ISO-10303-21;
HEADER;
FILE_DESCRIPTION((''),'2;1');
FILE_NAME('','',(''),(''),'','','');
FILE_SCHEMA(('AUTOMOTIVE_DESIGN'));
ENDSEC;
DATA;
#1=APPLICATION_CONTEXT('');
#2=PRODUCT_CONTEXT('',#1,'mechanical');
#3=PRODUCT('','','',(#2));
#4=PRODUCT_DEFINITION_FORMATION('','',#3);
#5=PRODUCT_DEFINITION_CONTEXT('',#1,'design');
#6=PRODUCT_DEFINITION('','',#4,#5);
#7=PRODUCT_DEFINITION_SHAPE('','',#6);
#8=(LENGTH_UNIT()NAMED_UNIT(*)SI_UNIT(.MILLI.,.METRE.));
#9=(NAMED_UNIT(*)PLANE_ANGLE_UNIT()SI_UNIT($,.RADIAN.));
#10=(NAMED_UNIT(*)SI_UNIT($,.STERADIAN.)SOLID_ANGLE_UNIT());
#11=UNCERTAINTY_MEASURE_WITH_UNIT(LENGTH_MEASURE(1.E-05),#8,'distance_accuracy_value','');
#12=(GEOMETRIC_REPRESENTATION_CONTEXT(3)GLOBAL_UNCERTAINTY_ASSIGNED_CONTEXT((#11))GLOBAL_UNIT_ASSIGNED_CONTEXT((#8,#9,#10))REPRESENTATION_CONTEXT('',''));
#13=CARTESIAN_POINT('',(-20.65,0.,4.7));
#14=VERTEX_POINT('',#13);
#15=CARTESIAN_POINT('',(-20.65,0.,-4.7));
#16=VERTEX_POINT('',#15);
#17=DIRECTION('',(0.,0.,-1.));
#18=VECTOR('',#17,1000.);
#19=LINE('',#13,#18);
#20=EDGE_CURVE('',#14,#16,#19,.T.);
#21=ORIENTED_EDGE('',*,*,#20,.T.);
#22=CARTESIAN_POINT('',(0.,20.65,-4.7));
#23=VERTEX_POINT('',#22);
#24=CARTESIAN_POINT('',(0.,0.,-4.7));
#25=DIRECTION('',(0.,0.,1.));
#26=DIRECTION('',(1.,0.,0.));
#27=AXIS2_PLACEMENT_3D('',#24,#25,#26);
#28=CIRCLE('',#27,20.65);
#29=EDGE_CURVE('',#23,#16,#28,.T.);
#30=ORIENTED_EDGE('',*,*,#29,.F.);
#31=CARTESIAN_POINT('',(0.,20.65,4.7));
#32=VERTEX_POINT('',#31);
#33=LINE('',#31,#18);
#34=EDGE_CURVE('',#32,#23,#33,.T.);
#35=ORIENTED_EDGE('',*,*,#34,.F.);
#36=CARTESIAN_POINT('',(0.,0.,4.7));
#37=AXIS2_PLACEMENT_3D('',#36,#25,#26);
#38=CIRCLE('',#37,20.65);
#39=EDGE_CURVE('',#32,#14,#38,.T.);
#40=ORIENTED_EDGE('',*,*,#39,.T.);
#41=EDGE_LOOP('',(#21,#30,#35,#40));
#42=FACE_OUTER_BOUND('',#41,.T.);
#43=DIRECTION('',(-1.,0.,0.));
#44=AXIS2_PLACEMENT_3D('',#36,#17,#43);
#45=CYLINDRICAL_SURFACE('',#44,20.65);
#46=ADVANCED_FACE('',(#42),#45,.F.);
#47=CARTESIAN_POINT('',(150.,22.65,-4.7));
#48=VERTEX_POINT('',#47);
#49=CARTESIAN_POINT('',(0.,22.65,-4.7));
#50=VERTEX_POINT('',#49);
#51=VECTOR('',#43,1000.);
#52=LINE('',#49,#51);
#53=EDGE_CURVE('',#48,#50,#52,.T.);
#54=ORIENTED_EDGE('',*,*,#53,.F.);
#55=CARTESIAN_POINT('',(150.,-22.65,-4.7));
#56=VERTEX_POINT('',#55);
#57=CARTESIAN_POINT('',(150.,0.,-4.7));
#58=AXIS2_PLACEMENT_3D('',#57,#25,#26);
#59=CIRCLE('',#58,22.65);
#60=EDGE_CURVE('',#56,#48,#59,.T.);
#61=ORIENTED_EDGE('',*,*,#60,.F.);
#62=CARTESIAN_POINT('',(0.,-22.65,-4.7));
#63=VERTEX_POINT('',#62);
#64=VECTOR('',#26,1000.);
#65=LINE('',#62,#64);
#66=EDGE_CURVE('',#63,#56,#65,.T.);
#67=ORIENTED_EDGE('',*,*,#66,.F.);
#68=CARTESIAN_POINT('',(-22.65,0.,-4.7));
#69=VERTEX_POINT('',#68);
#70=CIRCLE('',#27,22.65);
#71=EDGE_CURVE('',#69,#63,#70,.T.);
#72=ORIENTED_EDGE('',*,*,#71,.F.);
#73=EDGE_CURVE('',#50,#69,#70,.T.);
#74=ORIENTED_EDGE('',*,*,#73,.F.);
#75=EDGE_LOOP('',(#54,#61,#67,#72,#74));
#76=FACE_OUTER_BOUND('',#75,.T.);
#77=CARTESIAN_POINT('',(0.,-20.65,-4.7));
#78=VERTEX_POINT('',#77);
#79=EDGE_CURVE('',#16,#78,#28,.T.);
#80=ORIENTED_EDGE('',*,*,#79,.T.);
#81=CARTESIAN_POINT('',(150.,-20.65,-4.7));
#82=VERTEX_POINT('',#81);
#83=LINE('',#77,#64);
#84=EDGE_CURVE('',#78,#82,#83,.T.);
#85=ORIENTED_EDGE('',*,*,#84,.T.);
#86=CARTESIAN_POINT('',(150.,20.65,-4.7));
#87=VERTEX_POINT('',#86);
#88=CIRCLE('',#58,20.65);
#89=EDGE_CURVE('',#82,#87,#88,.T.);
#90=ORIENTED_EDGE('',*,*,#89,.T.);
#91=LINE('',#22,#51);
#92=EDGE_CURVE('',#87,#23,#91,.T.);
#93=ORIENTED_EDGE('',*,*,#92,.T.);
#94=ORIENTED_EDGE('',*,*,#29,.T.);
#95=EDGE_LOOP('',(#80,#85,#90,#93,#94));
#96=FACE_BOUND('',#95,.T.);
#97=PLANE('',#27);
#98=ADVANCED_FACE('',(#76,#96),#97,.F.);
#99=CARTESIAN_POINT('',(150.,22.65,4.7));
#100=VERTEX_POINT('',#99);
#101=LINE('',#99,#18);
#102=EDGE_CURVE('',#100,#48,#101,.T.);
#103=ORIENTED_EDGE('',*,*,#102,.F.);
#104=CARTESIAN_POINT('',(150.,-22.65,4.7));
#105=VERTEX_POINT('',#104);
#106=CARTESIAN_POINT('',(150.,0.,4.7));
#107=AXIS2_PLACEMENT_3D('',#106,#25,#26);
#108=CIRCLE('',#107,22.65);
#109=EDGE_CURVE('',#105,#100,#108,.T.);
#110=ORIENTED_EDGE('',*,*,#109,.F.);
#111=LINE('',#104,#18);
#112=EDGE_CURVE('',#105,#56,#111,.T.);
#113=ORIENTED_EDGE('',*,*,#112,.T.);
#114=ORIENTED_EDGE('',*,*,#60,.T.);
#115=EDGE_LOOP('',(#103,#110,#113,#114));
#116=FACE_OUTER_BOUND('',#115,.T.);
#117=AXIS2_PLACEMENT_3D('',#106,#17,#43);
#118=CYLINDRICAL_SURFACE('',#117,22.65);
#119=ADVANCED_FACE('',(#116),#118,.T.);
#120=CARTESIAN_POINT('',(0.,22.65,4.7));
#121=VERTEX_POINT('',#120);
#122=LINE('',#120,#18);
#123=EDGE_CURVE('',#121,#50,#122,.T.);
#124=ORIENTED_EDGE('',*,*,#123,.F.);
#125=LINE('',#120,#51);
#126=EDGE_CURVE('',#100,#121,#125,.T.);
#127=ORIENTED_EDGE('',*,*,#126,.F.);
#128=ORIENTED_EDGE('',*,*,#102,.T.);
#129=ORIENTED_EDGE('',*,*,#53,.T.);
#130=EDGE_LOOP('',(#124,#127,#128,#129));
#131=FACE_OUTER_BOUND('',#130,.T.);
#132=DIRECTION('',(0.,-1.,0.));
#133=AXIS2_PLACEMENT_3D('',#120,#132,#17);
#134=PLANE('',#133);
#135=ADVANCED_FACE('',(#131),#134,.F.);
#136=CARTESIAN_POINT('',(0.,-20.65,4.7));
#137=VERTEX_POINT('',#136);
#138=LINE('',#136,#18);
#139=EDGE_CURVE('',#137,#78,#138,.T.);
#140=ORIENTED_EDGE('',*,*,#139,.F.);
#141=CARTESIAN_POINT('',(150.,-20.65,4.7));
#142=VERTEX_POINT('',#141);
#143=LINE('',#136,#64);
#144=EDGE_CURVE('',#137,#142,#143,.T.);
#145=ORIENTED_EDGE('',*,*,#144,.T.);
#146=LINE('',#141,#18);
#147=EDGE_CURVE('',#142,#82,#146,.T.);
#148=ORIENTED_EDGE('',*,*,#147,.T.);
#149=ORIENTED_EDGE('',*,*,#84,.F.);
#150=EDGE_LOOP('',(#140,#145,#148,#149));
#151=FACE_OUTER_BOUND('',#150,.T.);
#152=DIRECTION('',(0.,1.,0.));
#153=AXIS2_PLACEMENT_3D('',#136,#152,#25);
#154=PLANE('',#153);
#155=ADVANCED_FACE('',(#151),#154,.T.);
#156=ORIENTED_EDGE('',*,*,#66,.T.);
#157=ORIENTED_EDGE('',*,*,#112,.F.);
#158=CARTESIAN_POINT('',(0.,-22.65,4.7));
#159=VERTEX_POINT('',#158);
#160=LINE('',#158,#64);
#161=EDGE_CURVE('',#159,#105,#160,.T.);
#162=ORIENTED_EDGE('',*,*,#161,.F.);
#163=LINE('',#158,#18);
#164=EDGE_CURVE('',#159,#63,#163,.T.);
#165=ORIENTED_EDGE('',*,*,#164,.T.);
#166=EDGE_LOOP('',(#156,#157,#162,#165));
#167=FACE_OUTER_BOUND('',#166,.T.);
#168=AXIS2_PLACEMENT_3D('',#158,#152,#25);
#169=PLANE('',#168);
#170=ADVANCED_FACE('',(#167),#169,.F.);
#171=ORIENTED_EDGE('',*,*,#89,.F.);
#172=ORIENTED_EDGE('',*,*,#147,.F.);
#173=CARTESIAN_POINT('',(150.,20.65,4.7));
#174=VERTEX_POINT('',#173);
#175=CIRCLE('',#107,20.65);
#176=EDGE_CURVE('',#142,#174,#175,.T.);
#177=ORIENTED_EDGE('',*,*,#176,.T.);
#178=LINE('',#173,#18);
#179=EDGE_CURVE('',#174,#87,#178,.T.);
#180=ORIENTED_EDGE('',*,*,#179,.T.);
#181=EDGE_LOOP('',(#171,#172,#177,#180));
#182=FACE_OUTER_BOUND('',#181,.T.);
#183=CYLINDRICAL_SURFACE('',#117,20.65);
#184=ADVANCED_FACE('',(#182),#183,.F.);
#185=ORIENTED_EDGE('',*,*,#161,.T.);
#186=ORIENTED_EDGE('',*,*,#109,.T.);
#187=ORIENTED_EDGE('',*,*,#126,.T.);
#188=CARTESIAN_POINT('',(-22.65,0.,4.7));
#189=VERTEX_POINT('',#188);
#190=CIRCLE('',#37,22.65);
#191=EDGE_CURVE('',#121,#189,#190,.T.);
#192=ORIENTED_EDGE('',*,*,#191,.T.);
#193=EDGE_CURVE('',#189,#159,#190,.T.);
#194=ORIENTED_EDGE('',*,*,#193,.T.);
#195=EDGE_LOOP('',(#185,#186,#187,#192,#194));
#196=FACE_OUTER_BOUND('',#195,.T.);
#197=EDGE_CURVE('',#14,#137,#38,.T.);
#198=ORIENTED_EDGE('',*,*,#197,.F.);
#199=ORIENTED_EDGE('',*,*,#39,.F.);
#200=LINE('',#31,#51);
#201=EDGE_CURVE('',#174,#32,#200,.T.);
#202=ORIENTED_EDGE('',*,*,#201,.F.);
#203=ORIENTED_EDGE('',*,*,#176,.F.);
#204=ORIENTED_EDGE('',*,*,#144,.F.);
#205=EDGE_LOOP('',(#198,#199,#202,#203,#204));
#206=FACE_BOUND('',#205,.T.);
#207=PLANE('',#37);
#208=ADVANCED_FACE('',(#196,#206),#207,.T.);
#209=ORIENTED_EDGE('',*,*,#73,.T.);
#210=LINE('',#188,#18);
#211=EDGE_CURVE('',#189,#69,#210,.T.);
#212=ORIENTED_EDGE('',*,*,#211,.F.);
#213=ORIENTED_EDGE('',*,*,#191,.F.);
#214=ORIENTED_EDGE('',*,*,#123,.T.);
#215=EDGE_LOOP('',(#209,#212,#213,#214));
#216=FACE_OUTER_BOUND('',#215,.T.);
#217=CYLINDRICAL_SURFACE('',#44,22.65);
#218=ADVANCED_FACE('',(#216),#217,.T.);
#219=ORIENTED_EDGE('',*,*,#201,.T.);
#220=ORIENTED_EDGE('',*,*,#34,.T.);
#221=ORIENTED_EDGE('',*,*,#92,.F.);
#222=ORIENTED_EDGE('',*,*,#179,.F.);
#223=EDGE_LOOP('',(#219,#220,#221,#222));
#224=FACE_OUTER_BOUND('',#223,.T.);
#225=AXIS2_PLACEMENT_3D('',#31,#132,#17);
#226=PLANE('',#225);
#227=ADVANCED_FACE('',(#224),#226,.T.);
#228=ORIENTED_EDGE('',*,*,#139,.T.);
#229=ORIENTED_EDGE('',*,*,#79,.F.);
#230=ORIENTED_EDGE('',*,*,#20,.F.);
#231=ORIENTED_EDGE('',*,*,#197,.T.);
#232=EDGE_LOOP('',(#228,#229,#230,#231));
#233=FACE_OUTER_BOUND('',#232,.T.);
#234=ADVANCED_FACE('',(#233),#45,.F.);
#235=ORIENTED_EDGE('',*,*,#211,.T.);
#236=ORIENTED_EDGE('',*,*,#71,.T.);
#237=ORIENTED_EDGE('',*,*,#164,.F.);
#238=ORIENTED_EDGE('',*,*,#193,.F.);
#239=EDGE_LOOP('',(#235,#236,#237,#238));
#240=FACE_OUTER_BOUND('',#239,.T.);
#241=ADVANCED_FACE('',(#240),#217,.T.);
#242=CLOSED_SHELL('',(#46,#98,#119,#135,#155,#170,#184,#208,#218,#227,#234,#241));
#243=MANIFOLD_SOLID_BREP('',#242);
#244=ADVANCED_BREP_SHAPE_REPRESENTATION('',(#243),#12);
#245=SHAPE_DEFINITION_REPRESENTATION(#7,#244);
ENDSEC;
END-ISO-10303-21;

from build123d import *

# Parameters (mm, degrees)
EXTRUDE_1_DEPTH = 4.7


with BuildPart() as part:
    # 草图1 → 拉伸-薄壁1 (new, symmetric)
    with BuildSketch(Plane.XY):
        with BuildLine():
            Line((150, -22.65), (0, -22.65))
            ThreePointArc((0, -22.65), (-22.65, 0), (0, 22.65))
            Line((0, 22.65), (150, 22.65))
            ThreePointArc((150, 22.65), (172.65, 0), (150, -22.65))
        make_face()
        with BuildLine():
            Line((150, -20.65), (0, -20.65))
            ThreePointArc((0, -20.65), (-20.65, 0), (0, 20.65))
            Line((0, 20.65), (150, 20.65))
            ThreePointArc((150, 20.65), (170.65, 0), (150, -20.65))
        make_face(mode=Mode.SUBTRACT)
    extrude(amount=EXTRUDE_1_DEPTH, both=True)


solid = part.part
